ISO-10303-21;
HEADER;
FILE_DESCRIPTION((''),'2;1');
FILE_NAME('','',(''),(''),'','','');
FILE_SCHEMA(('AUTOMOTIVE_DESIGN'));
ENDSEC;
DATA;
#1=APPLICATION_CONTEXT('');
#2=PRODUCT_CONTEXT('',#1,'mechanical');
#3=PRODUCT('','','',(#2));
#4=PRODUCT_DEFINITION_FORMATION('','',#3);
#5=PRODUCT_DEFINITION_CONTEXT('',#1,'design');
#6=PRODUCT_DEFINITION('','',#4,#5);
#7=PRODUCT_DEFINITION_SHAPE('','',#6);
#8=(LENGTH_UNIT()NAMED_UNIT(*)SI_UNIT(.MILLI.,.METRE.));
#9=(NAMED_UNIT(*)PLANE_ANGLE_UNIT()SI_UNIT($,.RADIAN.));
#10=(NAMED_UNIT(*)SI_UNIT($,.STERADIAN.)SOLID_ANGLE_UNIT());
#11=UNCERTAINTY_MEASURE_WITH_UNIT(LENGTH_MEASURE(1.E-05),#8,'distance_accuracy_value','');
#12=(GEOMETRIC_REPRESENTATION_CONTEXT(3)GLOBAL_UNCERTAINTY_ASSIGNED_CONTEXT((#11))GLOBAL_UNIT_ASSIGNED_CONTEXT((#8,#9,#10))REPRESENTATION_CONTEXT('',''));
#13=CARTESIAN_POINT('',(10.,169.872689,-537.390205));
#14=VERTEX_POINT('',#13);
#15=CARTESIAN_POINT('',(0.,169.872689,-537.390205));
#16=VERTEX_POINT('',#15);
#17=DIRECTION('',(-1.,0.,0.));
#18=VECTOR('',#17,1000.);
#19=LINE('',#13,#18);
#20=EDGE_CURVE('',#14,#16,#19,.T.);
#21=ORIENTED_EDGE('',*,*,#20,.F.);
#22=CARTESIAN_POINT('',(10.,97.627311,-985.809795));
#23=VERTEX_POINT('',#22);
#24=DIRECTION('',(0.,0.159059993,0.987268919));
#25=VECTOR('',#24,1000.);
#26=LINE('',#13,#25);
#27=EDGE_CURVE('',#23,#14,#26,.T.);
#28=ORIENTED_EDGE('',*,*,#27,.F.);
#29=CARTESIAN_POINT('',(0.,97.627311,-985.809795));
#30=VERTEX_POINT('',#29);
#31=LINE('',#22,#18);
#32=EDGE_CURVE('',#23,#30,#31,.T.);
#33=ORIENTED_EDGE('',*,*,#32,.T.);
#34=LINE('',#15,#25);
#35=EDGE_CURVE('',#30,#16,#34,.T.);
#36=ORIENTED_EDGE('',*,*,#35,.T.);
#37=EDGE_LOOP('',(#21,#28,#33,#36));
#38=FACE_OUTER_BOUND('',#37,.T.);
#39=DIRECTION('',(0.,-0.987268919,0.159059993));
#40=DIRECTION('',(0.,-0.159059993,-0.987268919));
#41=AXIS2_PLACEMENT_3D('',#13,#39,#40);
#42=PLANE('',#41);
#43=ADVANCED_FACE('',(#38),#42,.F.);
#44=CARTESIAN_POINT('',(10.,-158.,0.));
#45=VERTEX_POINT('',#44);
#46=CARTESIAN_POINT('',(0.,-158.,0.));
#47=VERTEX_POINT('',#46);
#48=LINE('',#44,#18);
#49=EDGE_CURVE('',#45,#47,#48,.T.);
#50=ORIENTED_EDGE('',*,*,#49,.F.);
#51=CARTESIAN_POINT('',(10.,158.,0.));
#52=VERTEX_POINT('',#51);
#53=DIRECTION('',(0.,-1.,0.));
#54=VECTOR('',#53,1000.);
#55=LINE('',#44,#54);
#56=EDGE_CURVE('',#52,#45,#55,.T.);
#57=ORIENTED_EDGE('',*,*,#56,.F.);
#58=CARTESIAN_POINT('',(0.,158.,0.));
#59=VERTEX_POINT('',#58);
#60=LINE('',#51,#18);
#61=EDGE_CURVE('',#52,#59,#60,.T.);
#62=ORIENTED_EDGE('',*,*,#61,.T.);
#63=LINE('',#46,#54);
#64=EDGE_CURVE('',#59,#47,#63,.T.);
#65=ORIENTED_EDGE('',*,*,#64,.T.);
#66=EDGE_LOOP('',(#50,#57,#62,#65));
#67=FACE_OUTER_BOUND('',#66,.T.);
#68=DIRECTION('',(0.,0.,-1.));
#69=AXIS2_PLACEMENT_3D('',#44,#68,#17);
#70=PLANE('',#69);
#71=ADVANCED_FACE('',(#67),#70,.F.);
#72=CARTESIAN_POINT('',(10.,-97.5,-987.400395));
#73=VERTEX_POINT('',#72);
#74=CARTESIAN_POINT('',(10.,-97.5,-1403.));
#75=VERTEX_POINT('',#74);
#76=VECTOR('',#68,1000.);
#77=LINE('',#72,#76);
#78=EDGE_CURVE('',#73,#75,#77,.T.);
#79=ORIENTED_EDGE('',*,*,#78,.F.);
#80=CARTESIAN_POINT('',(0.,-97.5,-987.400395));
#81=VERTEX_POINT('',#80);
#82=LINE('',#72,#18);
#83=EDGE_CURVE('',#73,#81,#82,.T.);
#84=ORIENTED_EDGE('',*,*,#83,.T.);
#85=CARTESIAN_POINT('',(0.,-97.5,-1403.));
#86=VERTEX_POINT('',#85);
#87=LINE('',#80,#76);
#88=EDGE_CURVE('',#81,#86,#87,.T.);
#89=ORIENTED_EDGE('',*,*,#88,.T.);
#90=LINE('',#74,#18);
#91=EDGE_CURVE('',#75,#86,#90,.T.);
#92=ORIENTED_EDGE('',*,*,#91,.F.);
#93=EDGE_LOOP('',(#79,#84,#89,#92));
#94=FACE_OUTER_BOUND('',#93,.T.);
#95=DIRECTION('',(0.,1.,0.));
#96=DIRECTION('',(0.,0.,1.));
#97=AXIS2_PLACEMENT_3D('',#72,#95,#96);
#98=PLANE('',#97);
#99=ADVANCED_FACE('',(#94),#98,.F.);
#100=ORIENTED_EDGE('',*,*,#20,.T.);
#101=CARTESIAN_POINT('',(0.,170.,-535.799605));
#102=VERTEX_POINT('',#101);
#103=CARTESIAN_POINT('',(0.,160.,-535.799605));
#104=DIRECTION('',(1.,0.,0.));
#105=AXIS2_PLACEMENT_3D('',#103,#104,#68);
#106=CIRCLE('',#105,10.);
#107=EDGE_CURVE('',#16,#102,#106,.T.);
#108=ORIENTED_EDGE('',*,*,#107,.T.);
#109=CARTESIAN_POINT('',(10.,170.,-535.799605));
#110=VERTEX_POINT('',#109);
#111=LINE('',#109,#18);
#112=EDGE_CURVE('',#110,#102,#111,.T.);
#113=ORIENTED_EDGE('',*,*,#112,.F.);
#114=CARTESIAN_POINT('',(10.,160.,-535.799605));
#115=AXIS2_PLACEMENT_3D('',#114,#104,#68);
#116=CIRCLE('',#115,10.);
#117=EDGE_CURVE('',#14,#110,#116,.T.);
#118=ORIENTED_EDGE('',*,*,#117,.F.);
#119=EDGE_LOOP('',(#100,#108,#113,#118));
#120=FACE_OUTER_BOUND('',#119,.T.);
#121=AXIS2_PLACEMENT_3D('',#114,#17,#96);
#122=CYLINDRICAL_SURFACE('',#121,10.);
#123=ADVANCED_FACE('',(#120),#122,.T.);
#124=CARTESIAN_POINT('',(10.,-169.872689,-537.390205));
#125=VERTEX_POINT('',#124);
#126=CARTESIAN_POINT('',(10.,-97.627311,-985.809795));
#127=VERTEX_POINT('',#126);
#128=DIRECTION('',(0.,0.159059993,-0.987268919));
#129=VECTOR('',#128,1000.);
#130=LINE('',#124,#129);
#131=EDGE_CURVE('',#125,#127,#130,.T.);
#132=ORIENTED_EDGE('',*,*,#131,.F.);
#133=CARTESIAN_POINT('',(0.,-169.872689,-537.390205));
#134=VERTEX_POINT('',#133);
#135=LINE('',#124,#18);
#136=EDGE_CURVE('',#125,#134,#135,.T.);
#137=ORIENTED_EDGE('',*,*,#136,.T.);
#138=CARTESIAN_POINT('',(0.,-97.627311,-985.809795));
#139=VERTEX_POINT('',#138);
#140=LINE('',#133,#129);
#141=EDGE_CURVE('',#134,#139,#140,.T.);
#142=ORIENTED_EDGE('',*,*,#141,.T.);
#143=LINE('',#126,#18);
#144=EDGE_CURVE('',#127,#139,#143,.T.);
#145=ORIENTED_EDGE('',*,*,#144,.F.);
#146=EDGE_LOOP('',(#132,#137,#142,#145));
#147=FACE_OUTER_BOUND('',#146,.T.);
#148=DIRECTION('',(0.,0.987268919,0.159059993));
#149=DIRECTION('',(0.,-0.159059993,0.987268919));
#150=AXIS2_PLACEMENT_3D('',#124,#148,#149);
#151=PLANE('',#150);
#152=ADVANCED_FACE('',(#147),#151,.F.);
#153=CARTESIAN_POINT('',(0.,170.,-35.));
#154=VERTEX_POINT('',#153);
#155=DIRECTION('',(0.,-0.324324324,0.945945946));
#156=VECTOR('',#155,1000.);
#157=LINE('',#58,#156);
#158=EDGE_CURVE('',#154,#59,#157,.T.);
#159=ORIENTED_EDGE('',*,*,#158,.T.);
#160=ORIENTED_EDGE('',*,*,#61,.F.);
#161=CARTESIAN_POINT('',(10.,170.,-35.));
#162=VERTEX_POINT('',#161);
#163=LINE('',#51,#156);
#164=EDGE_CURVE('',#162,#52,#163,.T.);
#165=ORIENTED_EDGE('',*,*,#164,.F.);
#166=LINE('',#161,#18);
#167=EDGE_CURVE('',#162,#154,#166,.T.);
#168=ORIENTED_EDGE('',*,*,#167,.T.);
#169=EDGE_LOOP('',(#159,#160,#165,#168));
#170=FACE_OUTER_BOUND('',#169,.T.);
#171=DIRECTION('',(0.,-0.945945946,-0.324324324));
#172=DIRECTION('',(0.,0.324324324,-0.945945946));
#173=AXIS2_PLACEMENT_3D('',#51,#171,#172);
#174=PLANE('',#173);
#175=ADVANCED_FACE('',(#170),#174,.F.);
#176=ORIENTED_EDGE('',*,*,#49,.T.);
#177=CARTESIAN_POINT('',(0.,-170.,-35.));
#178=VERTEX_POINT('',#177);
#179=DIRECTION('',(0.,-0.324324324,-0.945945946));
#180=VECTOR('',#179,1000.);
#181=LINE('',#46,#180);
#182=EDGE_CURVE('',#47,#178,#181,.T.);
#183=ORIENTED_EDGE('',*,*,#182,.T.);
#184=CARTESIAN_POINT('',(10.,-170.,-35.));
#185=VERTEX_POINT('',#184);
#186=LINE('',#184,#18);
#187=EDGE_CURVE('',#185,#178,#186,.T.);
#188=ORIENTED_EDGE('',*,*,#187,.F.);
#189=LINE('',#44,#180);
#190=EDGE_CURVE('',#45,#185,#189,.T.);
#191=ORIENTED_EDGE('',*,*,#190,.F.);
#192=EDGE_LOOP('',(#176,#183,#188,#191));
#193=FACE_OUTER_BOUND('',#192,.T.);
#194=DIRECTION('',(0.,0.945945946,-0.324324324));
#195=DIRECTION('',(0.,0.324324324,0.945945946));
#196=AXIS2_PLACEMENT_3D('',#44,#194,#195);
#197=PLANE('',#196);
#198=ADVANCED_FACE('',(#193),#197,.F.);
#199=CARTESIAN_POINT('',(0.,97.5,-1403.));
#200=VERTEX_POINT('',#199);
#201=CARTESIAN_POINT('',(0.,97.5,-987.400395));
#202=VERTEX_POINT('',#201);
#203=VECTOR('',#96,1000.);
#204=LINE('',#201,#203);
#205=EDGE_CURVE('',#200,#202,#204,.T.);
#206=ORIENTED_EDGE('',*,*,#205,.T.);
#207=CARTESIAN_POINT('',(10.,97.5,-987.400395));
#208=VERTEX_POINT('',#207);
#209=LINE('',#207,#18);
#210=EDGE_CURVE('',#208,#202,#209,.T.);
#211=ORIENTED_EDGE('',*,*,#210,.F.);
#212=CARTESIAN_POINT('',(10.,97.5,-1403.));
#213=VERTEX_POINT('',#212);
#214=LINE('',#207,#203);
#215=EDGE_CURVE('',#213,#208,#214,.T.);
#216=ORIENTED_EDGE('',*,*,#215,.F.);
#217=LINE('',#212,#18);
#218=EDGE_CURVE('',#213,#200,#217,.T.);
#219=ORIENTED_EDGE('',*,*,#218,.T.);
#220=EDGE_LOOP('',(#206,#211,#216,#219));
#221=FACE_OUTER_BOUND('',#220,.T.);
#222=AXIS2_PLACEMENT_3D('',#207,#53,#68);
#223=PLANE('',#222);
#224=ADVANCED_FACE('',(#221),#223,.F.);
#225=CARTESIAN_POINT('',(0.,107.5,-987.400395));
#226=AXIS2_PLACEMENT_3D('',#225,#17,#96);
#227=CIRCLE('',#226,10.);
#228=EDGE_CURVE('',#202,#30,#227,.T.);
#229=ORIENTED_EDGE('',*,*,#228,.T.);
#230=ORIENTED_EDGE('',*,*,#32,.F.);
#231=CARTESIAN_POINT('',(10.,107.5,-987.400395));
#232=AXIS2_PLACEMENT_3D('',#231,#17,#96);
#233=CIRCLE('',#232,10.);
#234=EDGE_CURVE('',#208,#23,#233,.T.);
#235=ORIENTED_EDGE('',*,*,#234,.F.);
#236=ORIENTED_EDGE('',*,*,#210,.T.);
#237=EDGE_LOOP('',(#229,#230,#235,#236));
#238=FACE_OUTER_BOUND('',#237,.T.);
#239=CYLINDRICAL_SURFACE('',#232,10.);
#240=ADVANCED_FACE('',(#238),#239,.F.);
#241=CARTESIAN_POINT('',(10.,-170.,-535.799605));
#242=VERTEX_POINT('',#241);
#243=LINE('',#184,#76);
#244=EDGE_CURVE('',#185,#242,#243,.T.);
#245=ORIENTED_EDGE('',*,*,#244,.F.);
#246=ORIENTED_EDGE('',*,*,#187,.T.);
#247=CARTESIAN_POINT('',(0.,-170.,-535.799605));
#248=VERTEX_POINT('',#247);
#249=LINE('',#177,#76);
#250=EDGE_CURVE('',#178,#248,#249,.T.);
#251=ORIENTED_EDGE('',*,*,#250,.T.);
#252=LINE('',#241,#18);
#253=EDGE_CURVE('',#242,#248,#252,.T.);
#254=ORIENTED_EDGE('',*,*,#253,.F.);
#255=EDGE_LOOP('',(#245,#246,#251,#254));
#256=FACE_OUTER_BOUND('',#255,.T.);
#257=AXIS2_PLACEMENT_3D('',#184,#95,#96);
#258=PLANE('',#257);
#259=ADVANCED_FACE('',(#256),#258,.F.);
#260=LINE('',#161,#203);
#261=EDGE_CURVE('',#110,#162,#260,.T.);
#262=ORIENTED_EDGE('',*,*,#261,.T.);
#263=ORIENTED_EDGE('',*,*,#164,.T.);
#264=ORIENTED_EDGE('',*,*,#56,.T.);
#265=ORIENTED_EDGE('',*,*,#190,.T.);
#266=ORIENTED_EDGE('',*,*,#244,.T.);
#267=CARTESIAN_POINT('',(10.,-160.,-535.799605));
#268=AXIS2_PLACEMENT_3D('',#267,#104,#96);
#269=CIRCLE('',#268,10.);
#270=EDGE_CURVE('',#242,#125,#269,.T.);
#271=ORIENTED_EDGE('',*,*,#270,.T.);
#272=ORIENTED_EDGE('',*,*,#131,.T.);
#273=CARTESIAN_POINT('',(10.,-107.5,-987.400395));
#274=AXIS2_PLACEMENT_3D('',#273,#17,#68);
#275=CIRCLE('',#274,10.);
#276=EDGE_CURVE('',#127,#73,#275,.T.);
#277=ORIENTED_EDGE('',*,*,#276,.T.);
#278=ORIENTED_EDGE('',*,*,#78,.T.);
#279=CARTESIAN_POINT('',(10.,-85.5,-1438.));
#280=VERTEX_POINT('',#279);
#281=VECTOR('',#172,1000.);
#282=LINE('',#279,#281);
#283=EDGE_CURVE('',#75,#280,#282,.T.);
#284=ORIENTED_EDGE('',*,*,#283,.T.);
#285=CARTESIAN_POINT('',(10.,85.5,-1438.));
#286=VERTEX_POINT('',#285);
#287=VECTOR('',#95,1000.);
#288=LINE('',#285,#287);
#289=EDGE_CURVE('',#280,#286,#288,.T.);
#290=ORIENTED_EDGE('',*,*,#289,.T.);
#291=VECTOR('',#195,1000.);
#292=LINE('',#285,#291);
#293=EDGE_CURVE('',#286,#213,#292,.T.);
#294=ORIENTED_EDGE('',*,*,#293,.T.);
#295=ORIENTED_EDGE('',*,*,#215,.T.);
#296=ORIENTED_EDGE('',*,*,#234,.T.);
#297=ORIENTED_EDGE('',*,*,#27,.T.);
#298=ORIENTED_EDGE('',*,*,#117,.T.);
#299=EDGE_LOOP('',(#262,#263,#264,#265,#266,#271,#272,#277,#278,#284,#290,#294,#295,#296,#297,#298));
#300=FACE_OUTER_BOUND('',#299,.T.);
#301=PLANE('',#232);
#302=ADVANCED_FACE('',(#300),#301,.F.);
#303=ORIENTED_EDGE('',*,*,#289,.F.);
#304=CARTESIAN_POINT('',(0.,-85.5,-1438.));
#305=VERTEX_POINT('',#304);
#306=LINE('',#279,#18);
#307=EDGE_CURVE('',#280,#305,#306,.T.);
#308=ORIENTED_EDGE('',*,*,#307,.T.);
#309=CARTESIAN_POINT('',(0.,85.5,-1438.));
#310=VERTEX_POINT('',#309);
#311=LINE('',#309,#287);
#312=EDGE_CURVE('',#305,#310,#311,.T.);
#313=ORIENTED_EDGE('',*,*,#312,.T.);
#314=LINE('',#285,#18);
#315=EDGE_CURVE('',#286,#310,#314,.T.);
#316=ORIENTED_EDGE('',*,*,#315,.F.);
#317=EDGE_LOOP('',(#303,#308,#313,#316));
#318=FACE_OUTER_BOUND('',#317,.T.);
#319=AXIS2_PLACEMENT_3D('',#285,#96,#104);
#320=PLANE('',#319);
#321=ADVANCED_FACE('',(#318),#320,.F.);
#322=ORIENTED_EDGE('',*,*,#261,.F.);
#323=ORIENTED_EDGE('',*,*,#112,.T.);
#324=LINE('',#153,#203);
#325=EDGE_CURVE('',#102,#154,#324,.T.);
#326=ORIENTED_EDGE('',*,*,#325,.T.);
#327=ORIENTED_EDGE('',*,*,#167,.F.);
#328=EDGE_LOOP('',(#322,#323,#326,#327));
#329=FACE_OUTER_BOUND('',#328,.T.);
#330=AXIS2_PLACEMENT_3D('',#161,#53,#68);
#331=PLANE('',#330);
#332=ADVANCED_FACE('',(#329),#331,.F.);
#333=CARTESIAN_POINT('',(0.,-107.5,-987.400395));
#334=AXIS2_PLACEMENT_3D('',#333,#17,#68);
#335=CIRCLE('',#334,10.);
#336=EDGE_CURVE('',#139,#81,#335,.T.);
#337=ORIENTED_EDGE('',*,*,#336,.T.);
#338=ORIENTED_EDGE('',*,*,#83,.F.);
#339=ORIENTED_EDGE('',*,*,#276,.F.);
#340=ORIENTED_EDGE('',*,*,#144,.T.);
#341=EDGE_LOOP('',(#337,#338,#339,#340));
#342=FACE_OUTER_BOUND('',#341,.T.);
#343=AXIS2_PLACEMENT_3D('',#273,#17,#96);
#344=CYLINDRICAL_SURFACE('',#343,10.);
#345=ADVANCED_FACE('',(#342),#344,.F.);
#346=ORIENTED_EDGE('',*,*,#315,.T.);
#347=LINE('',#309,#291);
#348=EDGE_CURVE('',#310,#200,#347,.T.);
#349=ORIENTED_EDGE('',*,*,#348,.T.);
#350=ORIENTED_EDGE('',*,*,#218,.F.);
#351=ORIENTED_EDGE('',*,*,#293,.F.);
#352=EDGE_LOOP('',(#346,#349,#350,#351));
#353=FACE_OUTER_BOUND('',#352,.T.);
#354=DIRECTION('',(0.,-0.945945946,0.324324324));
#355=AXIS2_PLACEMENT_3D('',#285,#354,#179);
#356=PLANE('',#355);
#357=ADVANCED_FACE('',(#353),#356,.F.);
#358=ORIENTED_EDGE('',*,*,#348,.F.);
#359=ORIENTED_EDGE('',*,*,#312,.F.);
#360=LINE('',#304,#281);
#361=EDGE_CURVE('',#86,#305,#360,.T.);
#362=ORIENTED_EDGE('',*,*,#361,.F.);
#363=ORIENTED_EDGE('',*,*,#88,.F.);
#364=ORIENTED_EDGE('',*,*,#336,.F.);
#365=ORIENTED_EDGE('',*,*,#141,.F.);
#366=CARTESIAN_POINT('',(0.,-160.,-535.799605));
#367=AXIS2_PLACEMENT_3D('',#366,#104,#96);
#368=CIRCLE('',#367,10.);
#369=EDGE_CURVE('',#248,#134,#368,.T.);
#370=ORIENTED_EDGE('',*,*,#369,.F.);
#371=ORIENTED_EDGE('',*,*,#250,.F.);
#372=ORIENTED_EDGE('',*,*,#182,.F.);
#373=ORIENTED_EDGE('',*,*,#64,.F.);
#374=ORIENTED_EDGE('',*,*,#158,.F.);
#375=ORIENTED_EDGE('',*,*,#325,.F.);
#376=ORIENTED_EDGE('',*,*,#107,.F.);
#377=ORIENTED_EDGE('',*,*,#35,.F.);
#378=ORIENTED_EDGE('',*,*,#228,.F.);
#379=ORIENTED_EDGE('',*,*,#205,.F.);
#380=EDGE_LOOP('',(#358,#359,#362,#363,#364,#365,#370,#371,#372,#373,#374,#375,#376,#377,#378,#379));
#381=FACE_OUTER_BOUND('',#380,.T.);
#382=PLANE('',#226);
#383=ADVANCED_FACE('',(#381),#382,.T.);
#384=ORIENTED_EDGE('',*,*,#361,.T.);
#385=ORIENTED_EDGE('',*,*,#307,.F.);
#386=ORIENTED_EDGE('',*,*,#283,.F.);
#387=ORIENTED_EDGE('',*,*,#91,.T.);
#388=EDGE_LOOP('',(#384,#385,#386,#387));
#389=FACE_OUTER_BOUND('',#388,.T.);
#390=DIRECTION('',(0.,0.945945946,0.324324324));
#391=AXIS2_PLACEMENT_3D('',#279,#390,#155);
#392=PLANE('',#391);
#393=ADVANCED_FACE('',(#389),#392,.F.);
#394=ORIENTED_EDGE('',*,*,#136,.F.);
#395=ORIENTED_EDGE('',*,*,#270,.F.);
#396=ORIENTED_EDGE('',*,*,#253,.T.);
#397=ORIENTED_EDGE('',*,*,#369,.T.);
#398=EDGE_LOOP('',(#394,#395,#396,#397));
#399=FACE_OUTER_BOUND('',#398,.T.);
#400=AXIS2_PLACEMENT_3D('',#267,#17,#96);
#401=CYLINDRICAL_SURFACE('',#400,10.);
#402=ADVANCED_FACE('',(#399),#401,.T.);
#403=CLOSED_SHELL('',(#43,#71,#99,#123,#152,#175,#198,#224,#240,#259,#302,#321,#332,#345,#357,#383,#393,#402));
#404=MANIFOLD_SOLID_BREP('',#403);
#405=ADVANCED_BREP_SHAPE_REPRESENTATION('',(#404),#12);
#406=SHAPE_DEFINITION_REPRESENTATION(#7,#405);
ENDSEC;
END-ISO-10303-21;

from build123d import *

# Parameters (mm, degrees)
BOSS_EXTRUDE1_DEPTH = 10


with BuildPart() as part:
    # Sketch1 → Boss-Extrude1 (new body)
    with BuildSketch(Plane(origin=(0, 0, 0), x_dir=(0, 0, -1), z_dir=(1, 0, 0))):
        with BuildLine():
            Line((0, -158), (0, 158))
            Line((0, 158), (35, 170))
            Line((35, 170), (535.799605091, 170))
            ThreePointArc((535.799605091, 170), (536.59744846, 169.968121486), (537.390205017, 169.872689192))
            Line((537.390205017, 169.872689192), (985.809794983, 97.627310808))
            ThreePointArc((985.809794983, 97.627310808), (986.60255154, 97.531878514), (987.400394909, 97.5))
            Line((987.400394909, 97.5), (1403, 97.5))
            Line((1403, 97.5), (1438, 85.5))
            Line((1438, 85.5), (1438, -85.5))
            Line((1438, -85.5), (1403, -97.5))
            Line((1403, -97.5), (987.400394909, -97.5))
            ThreePointArc((987.400394909, -97.5), (986.60255154, -97.531878514), (985.809794983, -97.627310808))
            Line((985.809794983, -97.627310808), (537.390205017, -169.872689192))
            ThreePointArc((537.390205017, -169.872689192), (536.59744846, -169.968121486), (535.799605091, -170))
            Line((535.799605091, -170), (35, -170))
            Line((35, -170), (0, -158))
        make_face()
    extrude(amount=BOSS_EXTRUDE1_DEPTH)


solid = part.part
